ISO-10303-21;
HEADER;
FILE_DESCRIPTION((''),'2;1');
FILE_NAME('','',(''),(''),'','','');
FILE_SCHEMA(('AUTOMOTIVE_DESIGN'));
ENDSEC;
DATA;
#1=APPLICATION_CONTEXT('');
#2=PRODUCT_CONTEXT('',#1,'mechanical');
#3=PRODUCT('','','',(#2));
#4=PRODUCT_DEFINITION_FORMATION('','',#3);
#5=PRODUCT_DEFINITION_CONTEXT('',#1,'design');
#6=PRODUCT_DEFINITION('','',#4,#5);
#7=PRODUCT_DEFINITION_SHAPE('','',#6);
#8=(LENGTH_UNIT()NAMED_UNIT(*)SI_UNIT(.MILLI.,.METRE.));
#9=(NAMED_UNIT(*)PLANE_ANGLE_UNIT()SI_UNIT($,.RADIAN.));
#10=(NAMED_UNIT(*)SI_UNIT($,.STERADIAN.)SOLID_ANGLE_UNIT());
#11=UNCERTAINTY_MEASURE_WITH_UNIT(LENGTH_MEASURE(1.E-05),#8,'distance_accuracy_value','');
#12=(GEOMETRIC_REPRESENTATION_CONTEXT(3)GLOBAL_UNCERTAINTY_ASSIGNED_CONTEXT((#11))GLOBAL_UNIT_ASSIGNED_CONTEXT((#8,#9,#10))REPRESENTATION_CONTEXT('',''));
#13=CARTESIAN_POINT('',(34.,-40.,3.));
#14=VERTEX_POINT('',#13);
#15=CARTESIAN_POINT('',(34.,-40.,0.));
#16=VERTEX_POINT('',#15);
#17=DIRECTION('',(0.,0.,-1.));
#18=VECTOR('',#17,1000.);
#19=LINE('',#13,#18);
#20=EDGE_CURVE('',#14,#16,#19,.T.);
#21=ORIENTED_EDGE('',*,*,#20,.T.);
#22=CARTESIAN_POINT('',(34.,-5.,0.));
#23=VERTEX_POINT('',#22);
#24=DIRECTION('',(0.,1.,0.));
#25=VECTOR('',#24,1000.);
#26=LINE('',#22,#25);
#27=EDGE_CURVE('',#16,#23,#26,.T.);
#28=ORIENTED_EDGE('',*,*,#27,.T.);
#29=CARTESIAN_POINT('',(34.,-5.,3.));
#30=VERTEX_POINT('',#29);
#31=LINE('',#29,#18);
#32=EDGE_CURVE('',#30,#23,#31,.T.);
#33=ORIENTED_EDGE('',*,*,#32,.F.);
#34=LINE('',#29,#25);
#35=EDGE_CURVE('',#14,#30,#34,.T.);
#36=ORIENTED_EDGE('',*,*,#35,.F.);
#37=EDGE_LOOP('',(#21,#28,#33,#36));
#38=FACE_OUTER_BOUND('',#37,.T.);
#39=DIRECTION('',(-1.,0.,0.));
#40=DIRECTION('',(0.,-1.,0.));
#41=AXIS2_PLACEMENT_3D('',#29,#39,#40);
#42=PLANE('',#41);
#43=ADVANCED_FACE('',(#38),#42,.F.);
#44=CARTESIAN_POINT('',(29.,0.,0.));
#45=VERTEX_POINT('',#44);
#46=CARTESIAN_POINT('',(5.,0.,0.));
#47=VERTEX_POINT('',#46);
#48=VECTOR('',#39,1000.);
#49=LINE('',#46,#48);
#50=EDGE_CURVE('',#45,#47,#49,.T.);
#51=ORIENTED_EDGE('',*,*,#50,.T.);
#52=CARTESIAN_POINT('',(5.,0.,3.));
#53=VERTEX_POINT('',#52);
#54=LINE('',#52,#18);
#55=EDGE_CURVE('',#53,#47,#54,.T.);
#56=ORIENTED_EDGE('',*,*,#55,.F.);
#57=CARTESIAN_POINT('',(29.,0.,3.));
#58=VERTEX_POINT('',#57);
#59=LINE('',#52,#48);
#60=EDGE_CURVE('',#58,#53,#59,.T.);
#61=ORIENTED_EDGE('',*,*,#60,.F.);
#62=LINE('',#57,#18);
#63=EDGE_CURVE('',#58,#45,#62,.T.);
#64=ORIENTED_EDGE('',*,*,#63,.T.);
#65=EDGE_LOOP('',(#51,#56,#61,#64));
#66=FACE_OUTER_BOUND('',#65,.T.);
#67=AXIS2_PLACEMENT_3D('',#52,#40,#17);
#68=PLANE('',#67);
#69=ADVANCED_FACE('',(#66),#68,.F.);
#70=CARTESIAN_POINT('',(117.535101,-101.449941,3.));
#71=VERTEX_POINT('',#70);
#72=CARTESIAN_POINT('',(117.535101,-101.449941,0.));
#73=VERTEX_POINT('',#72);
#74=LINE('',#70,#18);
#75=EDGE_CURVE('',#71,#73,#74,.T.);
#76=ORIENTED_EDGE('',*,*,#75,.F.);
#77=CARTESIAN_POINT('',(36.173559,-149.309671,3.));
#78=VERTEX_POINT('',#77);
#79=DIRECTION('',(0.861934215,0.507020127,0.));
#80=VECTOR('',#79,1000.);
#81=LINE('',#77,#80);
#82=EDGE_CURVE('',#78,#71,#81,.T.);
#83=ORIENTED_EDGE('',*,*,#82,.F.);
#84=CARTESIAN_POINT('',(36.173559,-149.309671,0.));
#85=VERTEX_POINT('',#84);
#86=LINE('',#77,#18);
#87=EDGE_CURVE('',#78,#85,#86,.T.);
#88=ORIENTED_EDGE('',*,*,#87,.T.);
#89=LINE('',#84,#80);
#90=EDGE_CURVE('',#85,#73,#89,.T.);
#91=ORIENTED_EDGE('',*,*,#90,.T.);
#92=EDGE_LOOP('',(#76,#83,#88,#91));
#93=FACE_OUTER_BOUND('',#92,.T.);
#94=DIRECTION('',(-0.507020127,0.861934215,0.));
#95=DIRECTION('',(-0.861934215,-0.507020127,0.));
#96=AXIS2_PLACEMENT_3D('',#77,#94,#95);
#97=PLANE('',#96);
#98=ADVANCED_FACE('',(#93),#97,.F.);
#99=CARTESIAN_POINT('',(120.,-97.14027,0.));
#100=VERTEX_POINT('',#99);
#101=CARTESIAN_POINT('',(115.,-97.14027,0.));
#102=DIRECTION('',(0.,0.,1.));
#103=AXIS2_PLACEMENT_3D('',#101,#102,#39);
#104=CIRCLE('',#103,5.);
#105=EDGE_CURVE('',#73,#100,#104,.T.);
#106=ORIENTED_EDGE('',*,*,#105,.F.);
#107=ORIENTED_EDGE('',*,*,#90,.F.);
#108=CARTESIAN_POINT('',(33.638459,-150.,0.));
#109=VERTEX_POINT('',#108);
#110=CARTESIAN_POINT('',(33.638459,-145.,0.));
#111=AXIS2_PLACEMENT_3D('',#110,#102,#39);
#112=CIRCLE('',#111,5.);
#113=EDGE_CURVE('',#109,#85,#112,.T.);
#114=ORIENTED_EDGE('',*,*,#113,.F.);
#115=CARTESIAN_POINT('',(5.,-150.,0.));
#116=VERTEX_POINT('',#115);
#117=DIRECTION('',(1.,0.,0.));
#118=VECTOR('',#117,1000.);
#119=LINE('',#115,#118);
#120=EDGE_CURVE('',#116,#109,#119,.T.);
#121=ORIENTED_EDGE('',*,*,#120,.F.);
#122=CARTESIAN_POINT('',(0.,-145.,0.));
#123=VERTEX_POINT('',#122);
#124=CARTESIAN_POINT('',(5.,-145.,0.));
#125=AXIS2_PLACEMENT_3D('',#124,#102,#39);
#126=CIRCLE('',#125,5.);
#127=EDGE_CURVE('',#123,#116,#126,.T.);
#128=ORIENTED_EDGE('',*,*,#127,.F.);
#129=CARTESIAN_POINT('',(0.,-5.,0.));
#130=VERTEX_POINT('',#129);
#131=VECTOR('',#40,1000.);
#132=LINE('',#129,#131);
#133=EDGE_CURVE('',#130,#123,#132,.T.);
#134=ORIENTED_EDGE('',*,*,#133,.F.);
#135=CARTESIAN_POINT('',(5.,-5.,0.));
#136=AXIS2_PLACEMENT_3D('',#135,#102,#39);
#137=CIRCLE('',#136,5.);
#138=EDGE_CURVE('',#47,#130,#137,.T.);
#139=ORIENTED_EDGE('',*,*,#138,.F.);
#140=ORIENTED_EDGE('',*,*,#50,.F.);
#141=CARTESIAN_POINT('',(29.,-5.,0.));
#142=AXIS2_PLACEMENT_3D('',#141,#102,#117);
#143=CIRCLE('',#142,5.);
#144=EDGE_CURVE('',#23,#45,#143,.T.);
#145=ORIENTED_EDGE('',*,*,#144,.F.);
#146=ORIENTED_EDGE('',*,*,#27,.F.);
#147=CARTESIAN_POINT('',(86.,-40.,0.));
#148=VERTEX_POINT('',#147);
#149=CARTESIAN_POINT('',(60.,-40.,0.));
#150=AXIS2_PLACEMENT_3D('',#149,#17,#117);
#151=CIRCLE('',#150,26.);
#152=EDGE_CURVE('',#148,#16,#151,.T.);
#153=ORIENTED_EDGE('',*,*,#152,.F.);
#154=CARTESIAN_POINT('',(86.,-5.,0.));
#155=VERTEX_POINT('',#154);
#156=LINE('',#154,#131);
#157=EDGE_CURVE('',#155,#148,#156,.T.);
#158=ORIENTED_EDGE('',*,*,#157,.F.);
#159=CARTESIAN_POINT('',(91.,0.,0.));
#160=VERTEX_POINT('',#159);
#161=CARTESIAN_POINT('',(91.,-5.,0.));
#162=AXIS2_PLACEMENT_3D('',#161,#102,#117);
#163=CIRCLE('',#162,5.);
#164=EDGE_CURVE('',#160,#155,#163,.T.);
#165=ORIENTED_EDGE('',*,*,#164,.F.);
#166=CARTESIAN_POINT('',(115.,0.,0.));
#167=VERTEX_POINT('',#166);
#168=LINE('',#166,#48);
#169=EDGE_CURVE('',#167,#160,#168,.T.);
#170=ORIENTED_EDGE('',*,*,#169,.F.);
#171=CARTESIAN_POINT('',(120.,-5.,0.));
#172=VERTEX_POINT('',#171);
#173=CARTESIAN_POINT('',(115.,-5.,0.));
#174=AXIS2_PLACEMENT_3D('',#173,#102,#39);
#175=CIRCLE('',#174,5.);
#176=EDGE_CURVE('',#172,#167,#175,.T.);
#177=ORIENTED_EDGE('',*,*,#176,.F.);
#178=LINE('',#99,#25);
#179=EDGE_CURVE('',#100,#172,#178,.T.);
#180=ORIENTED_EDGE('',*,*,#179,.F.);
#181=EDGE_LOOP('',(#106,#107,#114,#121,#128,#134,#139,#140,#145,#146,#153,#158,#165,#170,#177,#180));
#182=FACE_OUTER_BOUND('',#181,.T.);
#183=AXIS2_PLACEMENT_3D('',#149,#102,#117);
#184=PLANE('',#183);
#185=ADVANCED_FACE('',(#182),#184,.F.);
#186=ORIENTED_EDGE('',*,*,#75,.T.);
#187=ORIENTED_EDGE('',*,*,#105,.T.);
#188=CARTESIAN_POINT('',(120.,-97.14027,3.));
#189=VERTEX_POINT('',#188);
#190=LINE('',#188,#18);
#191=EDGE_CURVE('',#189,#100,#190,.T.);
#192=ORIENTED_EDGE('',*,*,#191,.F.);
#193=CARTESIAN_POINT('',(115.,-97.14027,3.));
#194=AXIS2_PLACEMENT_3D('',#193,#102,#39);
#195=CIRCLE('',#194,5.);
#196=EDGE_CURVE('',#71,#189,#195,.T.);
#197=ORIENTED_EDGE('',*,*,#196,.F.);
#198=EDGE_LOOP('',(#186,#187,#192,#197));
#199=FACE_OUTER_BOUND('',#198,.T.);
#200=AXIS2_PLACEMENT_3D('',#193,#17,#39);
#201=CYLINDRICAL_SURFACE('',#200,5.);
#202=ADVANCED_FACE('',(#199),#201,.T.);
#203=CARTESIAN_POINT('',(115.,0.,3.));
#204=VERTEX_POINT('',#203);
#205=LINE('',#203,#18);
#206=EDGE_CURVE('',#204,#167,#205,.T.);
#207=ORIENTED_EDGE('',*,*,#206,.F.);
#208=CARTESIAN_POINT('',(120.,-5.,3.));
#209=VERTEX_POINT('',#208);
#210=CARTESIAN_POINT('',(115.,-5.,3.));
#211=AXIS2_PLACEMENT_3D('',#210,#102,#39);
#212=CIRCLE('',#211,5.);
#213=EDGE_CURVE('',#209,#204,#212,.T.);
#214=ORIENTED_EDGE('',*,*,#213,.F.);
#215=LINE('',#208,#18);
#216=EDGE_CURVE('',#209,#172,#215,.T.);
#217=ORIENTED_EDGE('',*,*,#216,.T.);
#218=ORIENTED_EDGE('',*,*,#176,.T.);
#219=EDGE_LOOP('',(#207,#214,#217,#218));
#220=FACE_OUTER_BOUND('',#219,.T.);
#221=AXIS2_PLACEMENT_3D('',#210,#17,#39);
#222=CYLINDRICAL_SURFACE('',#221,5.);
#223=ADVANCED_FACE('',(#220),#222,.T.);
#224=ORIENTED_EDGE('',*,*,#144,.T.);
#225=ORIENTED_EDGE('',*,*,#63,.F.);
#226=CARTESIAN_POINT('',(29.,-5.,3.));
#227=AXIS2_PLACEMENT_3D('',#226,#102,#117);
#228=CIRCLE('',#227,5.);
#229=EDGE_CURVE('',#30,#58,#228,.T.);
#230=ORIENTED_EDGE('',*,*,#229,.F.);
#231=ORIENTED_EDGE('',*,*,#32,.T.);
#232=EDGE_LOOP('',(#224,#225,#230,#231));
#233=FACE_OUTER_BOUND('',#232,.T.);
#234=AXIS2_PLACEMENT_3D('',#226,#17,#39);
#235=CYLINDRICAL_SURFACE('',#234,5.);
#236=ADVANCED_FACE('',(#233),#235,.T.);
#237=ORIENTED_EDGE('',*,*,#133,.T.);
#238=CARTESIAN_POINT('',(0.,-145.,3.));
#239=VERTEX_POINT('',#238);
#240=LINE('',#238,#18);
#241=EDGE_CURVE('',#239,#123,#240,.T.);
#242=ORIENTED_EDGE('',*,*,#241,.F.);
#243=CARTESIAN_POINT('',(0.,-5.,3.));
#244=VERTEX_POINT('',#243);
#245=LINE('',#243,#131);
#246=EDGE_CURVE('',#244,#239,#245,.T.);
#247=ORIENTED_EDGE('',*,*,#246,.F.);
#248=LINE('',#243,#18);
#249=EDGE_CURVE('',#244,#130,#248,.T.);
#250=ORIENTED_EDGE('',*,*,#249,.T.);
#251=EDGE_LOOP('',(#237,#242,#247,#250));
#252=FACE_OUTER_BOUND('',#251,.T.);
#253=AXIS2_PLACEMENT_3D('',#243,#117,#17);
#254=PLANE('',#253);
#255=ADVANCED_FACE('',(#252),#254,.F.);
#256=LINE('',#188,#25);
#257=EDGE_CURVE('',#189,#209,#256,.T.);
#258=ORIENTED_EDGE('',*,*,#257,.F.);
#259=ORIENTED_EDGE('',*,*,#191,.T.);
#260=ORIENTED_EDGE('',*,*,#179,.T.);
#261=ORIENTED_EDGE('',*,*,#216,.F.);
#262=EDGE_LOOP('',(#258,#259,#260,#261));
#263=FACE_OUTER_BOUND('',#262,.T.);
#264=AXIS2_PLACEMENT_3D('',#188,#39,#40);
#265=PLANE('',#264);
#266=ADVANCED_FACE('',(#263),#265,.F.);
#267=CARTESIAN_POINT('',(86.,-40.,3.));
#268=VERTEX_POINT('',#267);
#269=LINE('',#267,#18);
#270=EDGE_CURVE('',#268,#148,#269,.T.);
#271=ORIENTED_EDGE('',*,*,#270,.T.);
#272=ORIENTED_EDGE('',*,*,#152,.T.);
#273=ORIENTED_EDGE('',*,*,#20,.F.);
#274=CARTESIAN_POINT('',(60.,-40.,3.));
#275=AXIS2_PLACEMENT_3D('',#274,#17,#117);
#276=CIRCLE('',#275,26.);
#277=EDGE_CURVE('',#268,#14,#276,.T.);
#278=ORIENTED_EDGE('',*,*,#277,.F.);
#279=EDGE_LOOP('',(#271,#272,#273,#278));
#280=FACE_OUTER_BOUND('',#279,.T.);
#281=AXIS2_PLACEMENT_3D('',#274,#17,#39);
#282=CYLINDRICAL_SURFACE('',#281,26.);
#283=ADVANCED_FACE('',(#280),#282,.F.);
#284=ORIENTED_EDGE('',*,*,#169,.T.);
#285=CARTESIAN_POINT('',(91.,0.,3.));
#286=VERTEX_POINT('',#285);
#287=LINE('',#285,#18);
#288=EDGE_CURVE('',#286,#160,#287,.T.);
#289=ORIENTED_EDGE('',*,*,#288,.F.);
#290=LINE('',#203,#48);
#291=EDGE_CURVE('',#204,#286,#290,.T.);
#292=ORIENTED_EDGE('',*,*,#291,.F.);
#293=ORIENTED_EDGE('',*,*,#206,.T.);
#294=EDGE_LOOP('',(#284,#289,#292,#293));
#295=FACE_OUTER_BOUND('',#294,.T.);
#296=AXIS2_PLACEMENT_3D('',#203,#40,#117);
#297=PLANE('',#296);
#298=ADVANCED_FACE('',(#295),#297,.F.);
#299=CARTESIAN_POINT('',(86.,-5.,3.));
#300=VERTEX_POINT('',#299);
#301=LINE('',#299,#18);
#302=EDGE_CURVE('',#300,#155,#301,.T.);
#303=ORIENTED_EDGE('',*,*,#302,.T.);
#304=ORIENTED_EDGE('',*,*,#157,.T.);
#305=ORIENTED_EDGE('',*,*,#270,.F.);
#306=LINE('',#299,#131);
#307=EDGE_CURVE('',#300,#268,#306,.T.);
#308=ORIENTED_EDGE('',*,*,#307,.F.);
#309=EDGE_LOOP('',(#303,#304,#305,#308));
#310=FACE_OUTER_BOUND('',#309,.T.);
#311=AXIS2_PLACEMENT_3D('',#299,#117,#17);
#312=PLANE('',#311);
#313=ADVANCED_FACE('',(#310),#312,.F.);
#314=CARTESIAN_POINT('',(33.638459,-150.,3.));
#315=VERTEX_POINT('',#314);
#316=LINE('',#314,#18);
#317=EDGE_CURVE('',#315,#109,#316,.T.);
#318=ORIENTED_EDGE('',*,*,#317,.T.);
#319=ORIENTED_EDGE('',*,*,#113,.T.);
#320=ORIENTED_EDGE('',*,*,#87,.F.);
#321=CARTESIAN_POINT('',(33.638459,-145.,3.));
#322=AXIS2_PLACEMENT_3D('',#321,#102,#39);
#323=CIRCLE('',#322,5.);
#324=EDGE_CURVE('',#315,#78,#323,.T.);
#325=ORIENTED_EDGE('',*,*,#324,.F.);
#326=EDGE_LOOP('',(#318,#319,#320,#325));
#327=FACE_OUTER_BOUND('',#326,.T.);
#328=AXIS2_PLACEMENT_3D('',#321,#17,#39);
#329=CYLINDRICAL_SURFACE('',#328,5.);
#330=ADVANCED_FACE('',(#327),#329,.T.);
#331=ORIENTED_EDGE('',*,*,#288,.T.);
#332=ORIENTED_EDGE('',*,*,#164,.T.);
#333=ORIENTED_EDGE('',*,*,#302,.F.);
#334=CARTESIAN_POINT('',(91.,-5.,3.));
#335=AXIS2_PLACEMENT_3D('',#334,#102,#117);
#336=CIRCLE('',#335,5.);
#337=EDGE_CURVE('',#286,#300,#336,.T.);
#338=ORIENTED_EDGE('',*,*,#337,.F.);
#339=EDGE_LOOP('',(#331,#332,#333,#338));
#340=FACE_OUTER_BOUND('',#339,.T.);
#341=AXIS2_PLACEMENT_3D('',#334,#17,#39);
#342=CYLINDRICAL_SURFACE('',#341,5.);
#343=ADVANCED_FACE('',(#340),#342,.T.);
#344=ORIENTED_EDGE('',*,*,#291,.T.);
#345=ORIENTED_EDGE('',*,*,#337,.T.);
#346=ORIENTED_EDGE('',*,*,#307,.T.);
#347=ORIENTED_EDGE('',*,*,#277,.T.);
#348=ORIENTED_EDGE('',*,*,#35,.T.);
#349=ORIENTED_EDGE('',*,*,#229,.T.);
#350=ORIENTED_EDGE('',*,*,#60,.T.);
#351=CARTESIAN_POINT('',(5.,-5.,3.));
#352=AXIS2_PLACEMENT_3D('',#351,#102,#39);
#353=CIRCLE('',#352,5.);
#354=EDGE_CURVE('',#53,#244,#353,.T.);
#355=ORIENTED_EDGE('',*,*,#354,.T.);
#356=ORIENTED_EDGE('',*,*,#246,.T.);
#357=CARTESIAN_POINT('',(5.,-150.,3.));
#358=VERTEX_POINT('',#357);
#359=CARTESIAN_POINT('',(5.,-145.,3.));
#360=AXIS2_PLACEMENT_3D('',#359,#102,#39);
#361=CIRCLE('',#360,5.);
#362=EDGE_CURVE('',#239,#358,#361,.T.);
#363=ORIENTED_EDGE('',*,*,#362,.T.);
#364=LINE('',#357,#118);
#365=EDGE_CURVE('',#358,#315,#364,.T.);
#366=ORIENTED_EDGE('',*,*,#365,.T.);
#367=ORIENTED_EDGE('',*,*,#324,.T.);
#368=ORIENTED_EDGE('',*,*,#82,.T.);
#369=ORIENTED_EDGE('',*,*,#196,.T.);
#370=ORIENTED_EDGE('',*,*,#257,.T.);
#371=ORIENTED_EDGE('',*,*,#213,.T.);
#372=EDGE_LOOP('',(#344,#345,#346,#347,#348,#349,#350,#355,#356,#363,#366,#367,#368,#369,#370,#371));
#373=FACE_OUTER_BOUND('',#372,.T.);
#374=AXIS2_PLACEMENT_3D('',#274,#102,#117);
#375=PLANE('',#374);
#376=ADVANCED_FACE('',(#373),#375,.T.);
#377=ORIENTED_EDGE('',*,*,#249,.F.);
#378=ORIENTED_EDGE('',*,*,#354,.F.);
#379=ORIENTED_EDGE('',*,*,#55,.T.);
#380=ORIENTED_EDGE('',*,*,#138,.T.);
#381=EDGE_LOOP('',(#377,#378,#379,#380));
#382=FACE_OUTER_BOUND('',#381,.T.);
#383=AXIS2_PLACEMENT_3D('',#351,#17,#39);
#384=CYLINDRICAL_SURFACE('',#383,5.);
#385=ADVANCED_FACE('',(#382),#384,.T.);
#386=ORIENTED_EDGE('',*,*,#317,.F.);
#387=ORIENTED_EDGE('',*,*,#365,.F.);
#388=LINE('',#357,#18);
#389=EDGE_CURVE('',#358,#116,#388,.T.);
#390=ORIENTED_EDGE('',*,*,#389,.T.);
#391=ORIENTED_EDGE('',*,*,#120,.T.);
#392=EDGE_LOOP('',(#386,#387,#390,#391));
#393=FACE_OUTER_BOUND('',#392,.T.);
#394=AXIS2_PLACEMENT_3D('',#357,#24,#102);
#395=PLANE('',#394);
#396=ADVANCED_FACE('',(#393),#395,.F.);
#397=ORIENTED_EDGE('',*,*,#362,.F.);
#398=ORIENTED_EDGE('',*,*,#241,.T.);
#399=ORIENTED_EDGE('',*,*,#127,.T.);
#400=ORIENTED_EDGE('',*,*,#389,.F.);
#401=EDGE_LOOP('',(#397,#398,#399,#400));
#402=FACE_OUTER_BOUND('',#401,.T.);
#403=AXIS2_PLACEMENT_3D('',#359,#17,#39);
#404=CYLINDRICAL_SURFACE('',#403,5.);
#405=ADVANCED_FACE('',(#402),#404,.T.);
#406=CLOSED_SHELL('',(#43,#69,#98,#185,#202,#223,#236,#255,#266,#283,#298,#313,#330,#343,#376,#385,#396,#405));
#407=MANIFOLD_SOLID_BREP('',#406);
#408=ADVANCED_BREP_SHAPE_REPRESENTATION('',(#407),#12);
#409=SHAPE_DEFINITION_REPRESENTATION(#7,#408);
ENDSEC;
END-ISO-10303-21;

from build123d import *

# Parameters (mm, degrees)
BOSS_EXTRUDE1_DEPTH = 3


with BuildPart() as part:
    # Sketch1 → Boss-Extrude1 (new body)
    with BuildSketch(Plane.XY):
        with BuildLine():
            Line((0, -5), (0, -145))
            ThreePointArc((0, -145), (1.464466094, -148.535533906), (5, -150))
            Line((5, -150), (33.638458538, -150))
            ThreePointArc((33.638458538, -150), (34.952164103, -149.824331839), (36.173559171, -149.309671076))
            Line((36.173559171, -149.309671076), (117.535100633, -101.449940804))
            ThreePointArc((117.535100633, -101.449940804), (119.340247871, -99.622657373), (120, -97.140269728))
            Line((120, -97.140269728), (120, -5))
            ThreePointArc((120, -5), (118.535533906, -1.464466094), (115, 0))
            Line((115, 0), (91, 0))
            ThreePointArc((91, 0), (87.464466094, -1.464466094), (86, -5))
            Line((86, -5), (86, -40))
            ThreePointArc((86, -40), (60, -66), (34, -40))
            Line((34, -40), (34, -5))
            ThreePointArc((34, -5), (32.535533906, -1.464466094), (29, 0))
            Line((29, 0), (5, 0))
            ThreePointArc((5, 0), (1.464466094, -1.464466094), (0, -5))
        make_face()
    extrude(amount=BOSS_EXTRUDE1_DEPTH)


solid = part.part
